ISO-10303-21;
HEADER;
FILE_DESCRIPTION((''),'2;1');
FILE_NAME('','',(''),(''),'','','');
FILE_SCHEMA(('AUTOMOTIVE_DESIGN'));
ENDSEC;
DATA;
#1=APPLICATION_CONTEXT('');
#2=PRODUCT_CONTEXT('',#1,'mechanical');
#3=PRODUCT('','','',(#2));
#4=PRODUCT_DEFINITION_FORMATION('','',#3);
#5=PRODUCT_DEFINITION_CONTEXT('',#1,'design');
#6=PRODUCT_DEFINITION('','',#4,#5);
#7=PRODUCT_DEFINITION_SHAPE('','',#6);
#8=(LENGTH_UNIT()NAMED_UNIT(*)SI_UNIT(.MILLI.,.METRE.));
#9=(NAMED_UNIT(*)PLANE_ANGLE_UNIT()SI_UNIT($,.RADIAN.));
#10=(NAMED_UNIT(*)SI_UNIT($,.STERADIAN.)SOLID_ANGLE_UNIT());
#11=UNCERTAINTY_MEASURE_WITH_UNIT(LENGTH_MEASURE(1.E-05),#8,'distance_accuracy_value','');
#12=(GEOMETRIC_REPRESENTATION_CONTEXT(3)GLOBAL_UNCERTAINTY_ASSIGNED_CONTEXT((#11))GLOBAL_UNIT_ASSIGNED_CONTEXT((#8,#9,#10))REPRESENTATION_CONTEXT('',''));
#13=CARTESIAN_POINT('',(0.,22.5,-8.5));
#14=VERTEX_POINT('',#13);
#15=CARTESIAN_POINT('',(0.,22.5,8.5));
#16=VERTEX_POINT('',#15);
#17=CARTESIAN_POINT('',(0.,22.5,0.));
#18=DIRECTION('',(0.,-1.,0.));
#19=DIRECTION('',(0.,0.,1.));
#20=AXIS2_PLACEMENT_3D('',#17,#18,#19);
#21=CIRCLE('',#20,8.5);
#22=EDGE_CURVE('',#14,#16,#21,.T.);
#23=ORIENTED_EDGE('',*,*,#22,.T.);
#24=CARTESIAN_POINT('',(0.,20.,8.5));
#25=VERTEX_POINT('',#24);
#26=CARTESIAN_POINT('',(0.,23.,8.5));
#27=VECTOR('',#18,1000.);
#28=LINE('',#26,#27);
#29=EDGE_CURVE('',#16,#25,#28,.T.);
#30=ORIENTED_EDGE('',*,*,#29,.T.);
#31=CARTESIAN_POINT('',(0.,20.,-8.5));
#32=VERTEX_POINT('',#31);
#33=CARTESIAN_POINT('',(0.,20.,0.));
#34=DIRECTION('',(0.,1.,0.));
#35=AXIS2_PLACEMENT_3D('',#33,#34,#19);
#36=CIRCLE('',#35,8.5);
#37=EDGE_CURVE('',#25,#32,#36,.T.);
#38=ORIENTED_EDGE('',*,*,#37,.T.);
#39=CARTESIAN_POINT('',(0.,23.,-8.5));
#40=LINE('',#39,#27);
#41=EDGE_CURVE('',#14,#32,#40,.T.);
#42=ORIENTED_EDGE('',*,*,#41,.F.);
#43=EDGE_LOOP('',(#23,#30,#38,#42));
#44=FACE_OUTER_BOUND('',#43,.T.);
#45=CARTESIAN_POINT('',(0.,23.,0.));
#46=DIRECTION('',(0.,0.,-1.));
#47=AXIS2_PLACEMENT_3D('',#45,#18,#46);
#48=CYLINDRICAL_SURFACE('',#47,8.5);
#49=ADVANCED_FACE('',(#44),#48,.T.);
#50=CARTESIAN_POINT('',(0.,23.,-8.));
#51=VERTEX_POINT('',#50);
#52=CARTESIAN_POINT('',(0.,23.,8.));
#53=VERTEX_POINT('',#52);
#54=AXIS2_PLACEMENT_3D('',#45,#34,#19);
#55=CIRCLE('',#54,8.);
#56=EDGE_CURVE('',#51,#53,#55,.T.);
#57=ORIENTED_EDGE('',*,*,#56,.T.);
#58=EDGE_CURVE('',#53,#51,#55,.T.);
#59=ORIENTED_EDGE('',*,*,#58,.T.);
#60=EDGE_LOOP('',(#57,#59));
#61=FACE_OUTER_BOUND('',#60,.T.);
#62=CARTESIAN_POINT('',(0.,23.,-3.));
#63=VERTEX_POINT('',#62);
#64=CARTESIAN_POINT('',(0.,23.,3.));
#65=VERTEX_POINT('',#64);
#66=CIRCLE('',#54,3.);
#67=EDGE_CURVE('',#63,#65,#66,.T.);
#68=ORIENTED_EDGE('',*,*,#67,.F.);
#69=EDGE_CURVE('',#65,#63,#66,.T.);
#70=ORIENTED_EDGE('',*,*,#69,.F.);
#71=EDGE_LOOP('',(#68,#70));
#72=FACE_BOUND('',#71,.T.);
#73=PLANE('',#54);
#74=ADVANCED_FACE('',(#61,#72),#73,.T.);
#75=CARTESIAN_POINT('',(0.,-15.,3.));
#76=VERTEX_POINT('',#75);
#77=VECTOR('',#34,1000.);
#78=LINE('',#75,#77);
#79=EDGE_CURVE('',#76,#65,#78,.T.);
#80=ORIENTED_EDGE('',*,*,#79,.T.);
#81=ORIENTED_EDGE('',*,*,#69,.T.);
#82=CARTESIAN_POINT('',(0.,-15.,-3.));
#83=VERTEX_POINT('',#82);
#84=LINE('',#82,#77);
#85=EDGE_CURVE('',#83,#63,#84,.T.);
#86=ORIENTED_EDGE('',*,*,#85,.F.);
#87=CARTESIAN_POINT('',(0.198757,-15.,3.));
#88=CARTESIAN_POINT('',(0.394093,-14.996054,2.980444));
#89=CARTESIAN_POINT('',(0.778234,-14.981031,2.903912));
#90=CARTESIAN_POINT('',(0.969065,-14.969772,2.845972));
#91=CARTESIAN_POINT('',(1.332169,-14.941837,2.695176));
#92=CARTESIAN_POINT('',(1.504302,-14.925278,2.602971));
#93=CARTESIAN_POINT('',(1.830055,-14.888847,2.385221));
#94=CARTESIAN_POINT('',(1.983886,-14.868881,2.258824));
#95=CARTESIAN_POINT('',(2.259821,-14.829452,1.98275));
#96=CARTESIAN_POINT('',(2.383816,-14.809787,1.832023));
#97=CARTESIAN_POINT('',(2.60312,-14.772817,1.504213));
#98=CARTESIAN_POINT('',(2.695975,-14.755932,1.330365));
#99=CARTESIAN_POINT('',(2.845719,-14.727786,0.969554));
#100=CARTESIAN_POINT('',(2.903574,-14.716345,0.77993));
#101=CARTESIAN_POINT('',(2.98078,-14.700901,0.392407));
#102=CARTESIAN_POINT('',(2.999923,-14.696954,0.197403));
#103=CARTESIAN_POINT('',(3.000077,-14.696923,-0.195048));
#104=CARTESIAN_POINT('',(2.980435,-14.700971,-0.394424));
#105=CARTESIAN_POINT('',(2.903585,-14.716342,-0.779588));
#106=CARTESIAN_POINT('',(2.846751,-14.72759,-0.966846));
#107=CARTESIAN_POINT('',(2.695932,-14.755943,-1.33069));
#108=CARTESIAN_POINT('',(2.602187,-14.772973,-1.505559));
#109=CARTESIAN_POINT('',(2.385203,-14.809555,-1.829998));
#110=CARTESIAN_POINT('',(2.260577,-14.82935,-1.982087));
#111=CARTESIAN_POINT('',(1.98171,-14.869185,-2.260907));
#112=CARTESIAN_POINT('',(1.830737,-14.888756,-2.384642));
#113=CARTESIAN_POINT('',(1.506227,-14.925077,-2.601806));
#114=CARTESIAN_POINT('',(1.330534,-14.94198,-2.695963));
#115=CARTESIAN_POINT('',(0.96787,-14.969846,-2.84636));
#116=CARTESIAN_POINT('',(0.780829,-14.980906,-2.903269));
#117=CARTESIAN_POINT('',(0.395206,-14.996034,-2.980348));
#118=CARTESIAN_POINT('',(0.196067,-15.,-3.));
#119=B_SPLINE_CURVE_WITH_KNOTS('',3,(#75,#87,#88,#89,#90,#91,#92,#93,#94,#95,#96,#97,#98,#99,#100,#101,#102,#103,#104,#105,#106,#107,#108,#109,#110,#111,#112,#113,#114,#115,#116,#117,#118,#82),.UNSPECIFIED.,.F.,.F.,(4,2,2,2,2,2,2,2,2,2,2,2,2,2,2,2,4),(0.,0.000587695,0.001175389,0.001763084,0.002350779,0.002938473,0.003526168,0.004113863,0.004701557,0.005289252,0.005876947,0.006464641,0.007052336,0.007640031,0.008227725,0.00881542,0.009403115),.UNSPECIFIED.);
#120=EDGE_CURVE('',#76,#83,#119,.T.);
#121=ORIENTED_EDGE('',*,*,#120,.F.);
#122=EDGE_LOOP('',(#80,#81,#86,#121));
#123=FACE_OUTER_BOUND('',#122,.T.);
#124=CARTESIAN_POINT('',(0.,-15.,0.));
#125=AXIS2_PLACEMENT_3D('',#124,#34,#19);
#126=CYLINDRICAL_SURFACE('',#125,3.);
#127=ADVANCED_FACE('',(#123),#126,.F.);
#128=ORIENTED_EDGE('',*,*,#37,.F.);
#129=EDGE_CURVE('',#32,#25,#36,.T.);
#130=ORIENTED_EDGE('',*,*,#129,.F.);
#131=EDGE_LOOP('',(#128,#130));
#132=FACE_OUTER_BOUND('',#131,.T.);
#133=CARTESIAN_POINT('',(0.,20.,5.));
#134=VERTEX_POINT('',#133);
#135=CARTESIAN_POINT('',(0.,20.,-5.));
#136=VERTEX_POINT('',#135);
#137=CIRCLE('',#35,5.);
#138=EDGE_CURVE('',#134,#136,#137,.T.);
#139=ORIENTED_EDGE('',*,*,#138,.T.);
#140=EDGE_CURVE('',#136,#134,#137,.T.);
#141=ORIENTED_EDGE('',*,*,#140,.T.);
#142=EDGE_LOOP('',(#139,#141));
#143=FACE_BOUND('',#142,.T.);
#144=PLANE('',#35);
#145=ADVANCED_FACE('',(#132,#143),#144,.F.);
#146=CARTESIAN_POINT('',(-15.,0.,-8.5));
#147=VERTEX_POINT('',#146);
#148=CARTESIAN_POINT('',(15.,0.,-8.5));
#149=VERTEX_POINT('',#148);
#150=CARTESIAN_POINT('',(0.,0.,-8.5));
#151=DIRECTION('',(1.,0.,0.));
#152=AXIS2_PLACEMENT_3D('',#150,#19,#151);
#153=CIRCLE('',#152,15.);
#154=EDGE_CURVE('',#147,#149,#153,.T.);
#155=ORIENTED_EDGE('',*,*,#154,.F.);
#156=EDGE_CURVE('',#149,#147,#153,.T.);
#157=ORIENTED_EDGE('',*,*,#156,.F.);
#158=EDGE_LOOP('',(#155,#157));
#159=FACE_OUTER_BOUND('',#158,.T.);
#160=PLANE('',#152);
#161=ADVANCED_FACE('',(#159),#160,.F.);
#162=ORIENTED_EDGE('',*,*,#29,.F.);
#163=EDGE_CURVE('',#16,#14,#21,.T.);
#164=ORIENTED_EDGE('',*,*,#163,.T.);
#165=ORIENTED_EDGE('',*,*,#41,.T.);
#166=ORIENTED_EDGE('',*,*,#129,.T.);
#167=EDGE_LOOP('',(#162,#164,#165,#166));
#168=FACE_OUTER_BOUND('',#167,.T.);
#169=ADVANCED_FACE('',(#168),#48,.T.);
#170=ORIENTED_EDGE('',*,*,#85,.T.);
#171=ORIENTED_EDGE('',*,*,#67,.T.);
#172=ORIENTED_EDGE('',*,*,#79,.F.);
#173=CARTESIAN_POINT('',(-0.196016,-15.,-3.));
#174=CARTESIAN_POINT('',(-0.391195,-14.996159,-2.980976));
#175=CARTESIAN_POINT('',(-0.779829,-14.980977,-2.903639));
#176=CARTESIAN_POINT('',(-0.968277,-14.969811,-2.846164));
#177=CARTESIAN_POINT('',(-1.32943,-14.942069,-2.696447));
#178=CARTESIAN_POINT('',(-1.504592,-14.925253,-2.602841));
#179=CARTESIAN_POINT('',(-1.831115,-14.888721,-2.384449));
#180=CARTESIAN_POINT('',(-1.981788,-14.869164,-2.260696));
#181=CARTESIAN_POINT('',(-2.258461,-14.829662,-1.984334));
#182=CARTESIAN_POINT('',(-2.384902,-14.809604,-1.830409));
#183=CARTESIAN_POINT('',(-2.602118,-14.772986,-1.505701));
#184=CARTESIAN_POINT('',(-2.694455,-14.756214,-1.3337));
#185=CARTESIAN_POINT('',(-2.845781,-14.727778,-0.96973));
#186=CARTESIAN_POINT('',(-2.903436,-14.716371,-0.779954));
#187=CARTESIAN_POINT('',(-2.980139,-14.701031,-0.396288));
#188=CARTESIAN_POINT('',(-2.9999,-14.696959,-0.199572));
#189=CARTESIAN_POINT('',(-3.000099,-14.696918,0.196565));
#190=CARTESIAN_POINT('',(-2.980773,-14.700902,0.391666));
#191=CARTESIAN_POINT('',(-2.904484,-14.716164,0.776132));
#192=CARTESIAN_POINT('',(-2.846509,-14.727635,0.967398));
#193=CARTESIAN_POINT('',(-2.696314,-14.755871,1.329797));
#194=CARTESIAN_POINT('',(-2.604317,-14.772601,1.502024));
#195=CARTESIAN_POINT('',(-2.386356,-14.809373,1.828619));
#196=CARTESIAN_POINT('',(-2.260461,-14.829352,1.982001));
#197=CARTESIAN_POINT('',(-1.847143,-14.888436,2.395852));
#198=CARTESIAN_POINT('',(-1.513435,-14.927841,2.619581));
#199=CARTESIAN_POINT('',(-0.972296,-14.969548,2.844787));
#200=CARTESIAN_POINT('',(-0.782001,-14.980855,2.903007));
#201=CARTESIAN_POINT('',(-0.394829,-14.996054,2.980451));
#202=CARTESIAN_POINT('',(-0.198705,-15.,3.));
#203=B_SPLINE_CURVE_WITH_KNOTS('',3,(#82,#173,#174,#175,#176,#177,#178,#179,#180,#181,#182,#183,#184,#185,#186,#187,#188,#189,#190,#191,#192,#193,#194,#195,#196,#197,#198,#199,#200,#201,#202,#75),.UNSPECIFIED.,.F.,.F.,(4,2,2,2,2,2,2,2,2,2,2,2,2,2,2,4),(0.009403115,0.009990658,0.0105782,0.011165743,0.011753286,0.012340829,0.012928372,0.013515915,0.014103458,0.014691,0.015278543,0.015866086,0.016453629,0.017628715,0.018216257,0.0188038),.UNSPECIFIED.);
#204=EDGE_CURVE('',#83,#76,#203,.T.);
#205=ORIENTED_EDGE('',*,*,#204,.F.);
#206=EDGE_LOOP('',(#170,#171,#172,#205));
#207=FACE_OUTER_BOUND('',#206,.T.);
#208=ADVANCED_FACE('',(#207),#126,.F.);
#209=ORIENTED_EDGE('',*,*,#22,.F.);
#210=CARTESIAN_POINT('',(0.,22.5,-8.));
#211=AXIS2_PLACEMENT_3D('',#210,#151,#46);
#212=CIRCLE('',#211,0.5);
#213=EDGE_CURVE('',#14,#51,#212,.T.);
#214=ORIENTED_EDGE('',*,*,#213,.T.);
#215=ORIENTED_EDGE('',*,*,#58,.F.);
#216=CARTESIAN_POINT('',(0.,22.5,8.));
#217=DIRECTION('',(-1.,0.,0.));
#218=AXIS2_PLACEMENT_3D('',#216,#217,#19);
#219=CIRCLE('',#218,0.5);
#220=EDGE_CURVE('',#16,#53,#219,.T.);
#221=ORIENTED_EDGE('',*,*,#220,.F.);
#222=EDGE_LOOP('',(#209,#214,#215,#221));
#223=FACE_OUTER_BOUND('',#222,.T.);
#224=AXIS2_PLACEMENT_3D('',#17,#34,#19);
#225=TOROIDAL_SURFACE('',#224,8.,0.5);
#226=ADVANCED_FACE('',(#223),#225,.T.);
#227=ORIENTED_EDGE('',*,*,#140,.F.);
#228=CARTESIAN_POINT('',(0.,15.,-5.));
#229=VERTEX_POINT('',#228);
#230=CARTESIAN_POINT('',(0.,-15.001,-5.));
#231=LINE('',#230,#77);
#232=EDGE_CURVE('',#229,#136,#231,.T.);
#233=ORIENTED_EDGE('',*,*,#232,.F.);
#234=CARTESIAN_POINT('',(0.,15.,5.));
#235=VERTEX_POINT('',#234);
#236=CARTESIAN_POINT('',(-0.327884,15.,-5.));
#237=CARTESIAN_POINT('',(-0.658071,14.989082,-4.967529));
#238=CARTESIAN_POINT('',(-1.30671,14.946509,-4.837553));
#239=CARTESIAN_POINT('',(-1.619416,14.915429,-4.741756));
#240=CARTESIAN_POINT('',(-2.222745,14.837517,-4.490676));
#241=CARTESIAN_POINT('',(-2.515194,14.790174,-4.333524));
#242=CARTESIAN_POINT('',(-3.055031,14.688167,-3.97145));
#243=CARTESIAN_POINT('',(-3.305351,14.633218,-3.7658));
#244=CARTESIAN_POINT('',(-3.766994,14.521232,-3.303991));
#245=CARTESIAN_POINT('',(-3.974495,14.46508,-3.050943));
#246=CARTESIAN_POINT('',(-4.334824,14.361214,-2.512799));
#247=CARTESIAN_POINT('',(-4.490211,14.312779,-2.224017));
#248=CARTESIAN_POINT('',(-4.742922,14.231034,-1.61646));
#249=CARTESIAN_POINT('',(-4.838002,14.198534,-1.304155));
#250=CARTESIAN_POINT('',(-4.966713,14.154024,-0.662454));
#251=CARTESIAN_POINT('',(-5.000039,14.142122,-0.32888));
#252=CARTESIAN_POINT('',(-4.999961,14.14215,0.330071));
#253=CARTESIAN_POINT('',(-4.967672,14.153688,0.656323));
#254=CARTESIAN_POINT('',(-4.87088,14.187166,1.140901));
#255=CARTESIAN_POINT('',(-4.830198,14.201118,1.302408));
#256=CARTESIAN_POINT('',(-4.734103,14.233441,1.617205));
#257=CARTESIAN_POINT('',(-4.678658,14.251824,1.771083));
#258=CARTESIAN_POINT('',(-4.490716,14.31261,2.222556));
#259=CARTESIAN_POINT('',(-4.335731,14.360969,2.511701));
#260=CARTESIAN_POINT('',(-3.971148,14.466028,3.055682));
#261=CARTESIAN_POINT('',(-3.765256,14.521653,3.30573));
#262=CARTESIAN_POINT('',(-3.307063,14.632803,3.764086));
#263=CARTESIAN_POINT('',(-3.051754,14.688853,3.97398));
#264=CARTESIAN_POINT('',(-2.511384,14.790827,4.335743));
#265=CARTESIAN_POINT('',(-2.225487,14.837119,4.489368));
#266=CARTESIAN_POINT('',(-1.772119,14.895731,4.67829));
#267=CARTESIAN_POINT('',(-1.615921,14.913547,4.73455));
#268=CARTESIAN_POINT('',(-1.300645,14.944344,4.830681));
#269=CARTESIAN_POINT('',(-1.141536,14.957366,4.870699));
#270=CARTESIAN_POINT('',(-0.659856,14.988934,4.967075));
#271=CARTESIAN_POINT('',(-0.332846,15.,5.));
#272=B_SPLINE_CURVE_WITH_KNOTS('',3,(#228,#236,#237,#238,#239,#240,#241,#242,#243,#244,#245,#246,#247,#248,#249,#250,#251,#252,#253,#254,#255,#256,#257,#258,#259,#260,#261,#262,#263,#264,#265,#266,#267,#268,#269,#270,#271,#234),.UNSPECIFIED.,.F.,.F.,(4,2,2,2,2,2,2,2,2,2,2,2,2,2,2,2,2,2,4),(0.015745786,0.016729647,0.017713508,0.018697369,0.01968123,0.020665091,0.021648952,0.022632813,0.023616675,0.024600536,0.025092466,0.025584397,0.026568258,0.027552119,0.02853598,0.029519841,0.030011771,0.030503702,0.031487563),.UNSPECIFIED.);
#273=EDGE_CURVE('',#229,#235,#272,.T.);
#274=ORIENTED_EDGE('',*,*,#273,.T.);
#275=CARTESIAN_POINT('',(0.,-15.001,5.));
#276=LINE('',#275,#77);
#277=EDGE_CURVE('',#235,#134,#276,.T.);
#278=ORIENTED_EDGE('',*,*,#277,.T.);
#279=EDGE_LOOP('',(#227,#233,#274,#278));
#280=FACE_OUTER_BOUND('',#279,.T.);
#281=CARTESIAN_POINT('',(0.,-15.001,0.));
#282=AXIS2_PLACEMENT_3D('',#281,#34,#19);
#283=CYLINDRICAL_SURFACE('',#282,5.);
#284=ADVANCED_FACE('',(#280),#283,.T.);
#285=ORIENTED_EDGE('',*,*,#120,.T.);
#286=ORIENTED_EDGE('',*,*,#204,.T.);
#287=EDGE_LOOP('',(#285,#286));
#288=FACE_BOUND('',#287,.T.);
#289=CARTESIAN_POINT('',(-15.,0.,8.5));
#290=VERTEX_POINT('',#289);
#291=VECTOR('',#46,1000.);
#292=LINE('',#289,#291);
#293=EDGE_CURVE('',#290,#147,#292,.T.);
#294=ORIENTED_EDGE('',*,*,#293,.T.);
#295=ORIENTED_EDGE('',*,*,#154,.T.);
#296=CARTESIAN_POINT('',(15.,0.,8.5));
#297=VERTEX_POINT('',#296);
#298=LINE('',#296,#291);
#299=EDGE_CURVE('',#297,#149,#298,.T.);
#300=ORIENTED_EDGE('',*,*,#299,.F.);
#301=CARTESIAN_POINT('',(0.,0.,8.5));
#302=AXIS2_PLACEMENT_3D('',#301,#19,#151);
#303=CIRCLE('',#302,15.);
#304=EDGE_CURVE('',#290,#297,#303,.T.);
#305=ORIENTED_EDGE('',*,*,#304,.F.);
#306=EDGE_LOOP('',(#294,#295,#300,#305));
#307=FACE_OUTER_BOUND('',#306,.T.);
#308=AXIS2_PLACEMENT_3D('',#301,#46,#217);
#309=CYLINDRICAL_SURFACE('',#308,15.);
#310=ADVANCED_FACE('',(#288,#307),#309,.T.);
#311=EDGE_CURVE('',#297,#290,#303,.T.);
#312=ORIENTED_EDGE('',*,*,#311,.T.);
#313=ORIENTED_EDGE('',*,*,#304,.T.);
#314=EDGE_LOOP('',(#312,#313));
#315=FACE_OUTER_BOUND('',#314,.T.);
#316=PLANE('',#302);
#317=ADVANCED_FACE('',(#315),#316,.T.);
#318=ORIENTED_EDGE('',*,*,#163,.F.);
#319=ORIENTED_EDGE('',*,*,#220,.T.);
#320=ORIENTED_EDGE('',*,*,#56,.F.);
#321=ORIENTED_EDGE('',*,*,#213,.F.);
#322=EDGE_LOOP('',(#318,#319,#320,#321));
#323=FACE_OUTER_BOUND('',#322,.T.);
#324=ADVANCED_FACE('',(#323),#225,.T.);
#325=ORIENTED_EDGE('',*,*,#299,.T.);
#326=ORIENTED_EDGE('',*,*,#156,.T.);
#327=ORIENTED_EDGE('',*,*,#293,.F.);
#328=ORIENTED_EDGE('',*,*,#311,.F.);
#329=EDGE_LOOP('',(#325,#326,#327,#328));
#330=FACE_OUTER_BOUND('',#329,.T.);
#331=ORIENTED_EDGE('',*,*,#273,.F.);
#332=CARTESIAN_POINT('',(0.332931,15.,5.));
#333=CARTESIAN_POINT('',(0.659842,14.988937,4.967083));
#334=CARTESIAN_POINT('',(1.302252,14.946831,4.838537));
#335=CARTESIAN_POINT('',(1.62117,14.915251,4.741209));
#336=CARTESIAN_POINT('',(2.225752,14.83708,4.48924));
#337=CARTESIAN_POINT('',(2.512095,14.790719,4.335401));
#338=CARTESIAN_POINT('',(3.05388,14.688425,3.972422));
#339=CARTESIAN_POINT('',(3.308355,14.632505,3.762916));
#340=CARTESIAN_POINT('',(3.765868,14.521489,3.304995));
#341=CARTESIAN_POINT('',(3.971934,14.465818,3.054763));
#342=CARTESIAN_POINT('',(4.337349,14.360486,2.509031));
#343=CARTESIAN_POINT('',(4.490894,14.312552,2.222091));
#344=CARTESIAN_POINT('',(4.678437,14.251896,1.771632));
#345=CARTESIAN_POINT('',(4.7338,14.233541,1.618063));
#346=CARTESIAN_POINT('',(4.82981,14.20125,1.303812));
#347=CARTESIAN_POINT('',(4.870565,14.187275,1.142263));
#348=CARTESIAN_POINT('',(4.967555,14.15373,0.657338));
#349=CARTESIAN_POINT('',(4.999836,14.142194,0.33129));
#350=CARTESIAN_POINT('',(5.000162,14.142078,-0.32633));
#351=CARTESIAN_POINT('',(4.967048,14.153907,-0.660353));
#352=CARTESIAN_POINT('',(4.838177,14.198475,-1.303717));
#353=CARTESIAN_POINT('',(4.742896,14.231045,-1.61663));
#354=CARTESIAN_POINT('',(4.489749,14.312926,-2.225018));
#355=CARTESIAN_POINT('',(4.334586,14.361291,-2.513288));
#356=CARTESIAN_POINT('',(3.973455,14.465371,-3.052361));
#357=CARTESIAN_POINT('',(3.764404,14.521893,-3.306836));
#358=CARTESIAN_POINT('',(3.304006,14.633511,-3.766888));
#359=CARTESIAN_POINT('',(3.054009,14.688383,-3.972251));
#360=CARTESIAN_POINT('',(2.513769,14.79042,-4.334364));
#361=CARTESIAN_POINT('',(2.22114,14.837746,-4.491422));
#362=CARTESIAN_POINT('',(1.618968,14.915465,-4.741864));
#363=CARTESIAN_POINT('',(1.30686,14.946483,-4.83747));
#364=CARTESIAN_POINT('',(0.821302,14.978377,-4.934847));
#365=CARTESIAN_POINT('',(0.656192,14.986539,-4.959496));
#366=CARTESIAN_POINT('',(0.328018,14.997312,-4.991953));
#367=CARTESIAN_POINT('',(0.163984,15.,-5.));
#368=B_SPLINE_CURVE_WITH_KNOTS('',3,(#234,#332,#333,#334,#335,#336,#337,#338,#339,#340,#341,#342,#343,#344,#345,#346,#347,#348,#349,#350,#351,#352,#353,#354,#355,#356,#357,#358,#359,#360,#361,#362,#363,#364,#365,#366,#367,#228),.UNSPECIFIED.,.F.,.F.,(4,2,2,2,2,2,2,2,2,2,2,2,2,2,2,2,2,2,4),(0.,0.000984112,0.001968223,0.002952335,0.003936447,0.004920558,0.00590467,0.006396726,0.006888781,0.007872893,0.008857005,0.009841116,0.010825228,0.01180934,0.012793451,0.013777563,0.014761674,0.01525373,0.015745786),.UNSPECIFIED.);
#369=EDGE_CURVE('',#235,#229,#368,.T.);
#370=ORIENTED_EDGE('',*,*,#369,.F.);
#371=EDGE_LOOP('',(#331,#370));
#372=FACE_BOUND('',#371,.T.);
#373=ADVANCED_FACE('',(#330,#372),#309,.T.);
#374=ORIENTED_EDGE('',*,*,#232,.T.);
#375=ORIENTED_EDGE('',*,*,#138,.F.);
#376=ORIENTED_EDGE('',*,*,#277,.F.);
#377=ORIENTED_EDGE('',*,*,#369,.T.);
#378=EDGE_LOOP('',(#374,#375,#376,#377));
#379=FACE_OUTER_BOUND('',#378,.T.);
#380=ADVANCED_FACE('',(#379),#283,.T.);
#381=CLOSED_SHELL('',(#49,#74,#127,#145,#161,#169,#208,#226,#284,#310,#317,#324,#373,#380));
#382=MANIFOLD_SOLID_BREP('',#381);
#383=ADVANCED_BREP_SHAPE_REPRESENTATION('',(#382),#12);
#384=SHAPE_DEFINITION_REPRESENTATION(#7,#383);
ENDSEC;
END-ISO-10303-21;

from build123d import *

# Parameters (mm, degrees)
SKETCH1_R                = 15
BOSS_EXTRUDE1_DEPTH      = 8.5
CUT_EXTRUDE1_DEPTH       = 23.852789764
CUT_EXTRUDE1_DEPTH_BACK  = 23.852789764
SKETCH2_R                = 3
BOSS_EXTRUDE2_REACH      = 41.016
BOSS_EXTRUDE2_END_RADIUS = 15
SKETCH3_R                = 5
SKETCH3_R_2              = 3
BOSS_EXTRUDE3_START      = 3
SKETCH4_R                = 8.5
SKETCH4_R_2              = 3
BOSS_EXTRUDE3_DEPTH      = 3
FILLET1_R                = 0.5


with BuildPart() as part:
    # Sketch1 → Boss-Extrude1 (new, symmetric)
    with BuildSketch(Plane.XY):
        Circle(SKETCH1_R)
    extrude(amount=BOSS_EXTRUDE1_DEPTH, both=True)

    # Sketch2 → Cut-Extrude1 (cut, two sides: drawn at the far end of the back side and taken through both)
    with BuildSketch(Plane(origin=(0, 0, 0), x_dir=(1, 0, 0), z_dir=(0, 1, 0)).offset(-CUT_EXTRUDE1_DEPTH_BACK)):
        with Locations(Location((0, 0, 0), (0, 0, 270))):
            Circle(SKETCH2_R)
    extrude(amount=CUT_EXTRUDE1_DEPTH + CUT_EXTRUDE1_DEPTH_BACK, mode=Mode.SUBTRACT)

    # Boss-Extrude2: up to this cylinder (the profile starts outside it)
    boss_extrude2_end = Plane(origin=(0, 0, -4.858579), z_dir=(0, 0, -1)) * Cylinder(BOSS_EXTRUDE2_END_RADIUS, 113.032, mode=Mode.PRIVATE)
    # Sketch3 → Boss-Extrude2 (add, up to the surface)
    with BuildSketch(Plane(origin=(0, 20, 0), x_dir=(1, 0, 0), z_dir=(0, 1, 0)), mode=Mode.PRIVATE) as boss_extrude2_sk1:
        with Locations(Location((0, 0, 0), (0, 0, 270))):
            Circle(SKETCH3_R)
        with Locations(Location((0, 0, 0), (0, 0, 270))):
            Circle(SKETCH3_R_2, mode=Mode.SUBTRACT)
    boss_extrude2_tool1 = extrude(boss_extrude2_sk1.sketch, amount=-BOSS_EXTRUDE2_REACH, mode=Mode.PRIVATE) - boss_extrude2_end
    add(boss_extrude2_tool1.solids().sort_by_distance((0, 20, -4.858579))[0])

    # Sketch4 → Boss-Extrude3 (add)
    with BuildSketch(Plane(origin=(0, 20, 0), x_dir=(1, 0, 0), z_dir=(0, 1, 0)).offset(BOSS_EXTRUDE3_START)):
        with Locations(Location((0, 0, 0), (0, 0, 270))):
            Circle(SKETCH4_R)
        with Locations(Location((0, 0, 0), (0, 0, 270))):
            Circle(SKETCH4_R_2, mode=Mode.SUBTRACT)
    extrude(amount=-BOSS_EXTRUDE3_DEPTH)

    # Fillet1
    fillet1_edges = [part.edges().sort_by_distance(p)[0] for p in [
        (0, 23, -8.5),
    ]]
    fillet(fillet1_edges, radius=FILLET1_R)


solid = part.part
